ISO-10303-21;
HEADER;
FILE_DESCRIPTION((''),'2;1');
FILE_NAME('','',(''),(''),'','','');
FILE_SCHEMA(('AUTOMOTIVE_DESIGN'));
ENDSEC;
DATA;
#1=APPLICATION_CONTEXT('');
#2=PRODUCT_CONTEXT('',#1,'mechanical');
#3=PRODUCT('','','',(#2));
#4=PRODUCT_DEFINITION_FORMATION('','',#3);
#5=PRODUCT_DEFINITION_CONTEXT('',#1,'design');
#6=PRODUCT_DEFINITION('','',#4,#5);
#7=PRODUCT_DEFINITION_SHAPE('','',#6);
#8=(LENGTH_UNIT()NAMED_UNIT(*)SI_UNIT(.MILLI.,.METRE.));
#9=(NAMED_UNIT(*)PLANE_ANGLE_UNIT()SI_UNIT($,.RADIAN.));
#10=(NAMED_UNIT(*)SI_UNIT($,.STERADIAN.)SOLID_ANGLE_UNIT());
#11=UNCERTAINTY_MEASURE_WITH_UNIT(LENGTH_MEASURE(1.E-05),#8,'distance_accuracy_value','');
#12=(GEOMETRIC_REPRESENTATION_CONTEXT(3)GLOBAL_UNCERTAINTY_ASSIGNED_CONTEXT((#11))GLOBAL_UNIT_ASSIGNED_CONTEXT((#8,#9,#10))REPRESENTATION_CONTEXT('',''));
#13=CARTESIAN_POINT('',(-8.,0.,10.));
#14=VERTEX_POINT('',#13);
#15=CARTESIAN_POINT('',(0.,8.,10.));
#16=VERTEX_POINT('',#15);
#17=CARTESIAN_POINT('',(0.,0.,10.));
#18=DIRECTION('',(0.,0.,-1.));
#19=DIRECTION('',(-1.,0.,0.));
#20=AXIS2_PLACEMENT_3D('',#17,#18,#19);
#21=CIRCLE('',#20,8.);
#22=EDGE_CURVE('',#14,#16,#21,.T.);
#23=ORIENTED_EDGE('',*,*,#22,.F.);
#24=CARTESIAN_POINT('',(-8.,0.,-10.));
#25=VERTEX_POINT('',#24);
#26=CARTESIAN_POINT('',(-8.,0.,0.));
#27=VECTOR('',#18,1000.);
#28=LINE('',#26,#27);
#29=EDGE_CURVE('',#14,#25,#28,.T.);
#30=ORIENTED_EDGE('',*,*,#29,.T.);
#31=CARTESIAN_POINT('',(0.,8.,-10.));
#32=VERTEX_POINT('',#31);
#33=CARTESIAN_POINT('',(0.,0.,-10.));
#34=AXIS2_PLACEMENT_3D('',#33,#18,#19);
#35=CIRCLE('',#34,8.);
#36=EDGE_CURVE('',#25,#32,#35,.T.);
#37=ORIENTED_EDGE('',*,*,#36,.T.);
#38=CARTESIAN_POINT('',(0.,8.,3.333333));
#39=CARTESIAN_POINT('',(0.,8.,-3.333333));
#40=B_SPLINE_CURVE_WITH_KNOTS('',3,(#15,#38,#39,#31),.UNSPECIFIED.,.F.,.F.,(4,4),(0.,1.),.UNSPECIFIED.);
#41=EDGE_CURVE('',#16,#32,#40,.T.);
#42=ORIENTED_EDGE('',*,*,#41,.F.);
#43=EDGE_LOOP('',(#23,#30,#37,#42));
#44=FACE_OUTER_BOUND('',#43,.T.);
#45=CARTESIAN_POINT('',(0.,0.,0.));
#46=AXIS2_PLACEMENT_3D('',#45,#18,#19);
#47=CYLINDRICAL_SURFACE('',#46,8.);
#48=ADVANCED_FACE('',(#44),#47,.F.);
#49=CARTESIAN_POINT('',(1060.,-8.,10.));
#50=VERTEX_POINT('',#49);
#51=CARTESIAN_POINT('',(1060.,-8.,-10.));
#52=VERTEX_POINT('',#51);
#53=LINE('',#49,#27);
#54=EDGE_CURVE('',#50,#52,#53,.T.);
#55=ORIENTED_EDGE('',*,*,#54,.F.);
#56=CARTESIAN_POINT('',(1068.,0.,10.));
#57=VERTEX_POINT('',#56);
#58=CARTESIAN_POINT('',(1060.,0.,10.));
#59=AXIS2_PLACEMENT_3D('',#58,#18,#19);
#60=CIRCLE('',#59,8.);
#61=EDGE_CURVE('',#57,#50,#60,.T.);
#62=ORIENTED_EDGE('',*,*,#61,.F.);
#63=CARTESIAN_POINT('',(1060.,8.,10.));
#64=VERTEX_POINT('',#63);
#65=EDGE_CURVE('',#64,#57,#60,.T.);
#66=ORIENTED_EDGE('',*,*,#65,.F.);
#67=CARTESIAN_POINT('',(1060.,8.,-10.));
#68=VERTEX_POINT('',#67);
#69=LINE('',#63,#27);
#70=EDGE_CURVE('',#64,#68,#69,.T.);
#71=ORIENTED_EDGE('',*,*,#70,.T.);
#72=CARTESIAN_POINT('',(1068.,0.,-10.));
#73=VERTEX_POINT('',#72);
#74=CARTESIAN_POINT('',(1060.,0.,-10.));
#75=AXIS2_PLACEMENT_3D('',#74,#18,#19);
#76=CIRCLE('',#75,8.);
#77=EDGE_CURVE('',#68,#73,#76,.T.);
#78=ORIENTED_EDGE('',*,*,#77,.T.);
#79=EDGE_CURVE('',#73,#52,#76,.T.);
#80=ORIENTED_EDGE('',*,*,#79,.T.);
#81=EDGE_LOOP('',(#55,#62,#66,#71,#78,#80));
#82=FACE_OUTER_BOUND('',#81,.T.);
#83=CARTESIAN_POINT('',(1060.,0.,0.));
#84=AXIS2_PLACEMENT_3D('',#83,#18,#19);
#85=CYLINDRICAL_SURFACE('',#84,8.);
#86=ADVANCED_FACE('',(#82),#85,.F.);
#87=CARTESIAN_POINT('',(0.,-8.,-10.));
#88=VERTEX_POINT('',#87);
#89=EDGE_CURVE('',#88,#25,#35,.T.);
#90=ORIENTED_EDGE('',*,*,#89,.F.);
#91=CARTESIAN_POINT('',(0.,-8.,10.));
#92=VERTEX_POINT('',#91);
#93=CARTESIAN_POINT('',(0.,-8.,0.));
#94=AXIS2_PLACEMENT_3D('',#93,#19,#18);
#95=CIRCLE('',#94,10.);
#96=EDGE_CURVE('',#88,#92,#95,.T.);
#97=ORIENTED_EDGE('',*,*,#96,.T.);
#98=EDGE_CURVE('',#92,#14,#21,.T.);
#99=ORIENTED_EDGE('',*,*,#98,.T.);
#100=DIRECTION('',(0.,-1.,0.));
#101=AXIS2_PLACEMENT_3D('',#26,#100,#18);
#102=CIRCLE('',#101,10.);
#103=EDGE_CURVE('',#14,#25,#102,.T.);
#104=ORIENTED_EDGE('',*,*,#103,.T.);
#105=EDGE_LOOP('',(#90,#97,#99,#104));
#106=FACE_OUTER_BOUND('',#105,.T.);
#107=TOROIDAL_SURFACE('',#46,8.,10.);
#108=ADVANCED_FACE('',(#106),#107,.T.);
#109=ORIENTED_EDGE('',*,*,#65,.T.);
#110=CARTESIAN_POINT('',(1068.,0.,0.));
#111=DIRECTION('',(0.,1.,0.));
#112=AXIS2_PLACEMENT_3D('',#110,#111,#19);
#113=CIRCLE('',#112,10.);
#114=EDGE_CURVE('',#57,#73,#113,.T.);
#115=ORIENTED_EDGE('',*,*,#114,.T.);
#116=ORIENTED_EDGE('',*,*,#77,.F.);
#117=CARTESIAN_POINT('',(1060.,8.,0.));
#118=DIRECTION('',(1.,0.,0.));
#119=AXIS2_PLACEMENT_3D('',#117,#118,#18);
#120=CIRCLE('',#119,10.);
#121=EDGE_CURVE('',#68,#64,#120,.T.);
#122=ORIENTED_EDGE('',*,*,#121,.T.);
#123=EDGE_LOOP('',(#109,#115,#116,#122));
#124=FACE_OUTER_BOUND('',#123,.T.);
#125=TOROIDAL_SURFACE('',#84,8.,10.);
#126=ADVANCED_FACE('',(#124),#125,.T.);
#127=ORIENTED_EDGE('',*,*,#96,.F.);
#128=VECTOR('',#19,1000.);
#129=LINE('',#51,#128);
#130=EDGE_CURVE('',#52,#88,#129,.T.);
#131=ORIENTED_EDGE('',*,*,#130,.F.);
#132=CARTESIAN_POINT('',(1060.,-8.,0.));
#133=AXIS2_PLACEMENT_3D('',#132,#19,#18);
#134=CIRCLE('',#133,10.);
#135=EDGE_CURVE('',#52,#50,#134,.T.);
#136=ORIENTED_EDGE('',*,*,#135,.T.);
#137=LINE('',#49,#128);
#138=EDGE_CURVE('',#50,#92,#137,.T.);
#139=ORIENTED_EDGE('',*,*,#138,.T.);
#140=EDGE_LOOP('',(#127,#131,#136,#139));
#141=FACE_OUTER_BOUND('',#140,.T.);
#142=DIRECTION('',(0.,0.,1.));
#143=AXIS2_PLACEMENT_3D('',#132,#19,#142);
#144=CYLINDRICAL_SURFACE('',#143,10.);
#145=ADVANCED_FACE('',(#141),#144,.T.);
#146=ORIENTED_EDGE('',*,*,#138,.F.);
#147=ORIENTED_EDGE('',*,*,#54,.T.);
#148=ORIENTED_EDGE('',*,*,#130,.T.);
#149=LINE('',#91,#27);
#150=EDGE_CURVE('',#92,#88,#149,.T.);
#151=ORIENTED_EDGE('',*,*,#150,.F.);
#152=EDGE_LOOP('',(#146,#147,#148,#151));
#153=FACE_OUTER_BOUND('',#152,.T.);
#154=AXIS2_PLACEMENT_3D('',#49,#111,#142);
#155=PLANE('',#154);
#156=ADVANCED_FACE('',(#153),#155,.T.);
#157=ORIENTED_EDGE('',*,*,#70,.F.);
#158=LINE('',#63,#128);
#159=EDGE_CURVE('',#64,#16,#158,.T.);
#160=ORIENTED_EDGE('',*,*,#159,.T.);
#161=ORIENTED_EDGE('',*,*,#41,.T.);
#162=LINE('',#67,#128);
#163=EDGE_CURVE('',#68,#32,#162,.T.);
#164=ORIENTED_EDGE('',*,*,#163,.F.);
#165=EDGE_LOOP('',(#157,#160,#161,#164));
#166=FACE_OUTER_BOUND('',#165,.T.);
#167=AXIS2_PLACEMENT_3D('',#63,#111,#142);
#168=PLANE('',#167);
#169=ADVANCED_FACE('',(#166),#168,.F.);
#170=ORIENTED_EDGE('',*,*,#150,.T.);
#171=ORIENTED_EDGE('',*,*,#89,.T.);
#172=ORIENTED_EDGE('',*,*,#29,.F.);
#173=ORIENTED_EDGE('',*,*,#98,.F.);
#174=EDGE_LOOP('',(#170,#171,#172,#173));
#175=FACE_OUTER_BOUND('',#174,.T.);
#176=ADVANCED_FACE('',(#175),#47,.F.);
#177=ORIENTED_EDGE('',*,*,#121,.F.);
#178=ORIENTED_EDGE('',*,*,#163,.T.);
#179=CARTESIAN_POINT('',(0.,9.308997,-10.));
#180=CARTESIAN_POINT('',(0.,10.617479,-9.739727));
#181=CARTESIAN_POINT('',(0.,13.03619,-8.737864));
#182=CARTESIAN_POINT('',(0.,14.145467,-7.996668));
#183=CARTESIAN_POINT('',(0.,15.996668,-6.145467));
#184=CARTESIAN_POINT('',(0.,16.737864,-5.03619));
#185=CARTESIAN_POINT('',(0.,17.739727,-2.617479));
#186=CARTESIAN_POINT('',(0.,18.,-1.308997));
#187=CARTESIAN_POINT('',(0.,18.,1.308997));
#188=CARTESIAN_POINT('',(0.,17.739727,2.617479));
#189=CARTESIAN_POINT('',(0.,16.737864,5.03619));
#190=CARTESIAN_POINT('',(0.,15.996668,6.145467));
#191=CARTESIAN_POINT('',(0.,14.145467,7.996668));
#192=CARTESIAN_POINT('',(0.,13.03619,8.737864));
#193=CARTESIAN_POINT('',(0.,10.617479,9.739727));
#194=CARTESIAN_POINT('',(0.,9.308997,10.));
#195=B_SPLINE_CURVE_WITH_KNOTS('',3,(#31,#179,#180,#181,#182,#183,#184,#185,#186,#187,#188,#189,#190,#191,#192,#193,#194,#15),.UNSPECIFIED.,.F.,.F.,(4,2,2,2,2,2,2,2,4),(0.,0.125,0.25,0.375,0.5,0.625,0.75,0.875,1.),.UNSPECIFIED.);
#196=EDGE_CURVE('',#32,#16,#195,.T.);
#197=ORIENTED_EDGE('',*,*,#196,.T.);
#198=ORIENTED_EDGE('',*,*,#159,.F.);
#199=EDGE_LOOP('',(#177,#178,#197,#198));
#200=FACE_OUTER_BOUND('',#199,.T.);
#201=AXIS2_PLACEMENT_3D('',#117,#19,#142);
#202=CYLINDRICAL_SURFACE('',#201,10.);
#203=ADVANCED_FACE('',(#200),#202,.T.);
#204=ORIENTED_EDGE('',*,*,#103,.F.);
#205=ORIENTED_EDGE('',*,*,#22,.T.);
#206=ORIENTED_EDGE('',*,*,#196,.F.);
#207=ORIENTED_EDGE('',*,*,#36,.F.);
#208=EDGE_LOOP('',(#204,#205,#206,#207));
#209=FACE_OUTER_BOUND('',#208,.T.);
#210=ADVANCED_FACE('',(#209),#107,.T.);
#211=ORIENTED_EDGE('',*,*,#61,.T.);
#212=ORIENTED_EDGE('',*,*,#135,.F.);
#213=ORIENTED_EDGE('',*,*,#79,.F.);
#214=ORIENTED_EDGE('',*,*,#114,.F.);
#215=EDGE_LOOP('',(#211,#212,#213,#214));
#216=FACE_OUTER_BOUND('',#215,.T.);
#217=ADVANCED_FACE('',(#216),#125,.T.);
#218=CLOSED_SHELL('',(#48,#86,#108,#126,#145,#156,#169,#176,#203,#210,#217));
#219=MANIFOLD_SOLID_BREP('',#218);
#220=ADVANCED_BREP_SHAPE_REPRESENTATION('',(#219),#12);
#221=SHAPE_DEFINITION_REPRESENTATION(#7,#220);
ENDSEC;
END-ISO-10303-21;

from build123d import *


with BuildPart() as part:
    # Sweep1: sweep along a path in Sketch1
    with BuildLine(Plane.XY) as sweep1_path:
        Line((0, 8), (1060, 8))
        ThreePointArc((1060, 8), (1068, 0), (1060, -8))
        Line((1060, -8), (0, -8))
        ThreePointArc((0, -8), (-8, 0), (0, 8))
    # Sketch2 → Sweep1 (sweep)
    with BuildSketch(Plane(origin=(0, 0, 0), x_dir=(0, 0, -1), z_dir=(1, 0, 0))):
        with BuildLine():
            Line((-10, 8), (10, 8))
            ThreePointArc((10, 8), (0, 18), (-10, 8))
        make_face()
    sweep(path=sweep1_path.line)


solid = part.part
